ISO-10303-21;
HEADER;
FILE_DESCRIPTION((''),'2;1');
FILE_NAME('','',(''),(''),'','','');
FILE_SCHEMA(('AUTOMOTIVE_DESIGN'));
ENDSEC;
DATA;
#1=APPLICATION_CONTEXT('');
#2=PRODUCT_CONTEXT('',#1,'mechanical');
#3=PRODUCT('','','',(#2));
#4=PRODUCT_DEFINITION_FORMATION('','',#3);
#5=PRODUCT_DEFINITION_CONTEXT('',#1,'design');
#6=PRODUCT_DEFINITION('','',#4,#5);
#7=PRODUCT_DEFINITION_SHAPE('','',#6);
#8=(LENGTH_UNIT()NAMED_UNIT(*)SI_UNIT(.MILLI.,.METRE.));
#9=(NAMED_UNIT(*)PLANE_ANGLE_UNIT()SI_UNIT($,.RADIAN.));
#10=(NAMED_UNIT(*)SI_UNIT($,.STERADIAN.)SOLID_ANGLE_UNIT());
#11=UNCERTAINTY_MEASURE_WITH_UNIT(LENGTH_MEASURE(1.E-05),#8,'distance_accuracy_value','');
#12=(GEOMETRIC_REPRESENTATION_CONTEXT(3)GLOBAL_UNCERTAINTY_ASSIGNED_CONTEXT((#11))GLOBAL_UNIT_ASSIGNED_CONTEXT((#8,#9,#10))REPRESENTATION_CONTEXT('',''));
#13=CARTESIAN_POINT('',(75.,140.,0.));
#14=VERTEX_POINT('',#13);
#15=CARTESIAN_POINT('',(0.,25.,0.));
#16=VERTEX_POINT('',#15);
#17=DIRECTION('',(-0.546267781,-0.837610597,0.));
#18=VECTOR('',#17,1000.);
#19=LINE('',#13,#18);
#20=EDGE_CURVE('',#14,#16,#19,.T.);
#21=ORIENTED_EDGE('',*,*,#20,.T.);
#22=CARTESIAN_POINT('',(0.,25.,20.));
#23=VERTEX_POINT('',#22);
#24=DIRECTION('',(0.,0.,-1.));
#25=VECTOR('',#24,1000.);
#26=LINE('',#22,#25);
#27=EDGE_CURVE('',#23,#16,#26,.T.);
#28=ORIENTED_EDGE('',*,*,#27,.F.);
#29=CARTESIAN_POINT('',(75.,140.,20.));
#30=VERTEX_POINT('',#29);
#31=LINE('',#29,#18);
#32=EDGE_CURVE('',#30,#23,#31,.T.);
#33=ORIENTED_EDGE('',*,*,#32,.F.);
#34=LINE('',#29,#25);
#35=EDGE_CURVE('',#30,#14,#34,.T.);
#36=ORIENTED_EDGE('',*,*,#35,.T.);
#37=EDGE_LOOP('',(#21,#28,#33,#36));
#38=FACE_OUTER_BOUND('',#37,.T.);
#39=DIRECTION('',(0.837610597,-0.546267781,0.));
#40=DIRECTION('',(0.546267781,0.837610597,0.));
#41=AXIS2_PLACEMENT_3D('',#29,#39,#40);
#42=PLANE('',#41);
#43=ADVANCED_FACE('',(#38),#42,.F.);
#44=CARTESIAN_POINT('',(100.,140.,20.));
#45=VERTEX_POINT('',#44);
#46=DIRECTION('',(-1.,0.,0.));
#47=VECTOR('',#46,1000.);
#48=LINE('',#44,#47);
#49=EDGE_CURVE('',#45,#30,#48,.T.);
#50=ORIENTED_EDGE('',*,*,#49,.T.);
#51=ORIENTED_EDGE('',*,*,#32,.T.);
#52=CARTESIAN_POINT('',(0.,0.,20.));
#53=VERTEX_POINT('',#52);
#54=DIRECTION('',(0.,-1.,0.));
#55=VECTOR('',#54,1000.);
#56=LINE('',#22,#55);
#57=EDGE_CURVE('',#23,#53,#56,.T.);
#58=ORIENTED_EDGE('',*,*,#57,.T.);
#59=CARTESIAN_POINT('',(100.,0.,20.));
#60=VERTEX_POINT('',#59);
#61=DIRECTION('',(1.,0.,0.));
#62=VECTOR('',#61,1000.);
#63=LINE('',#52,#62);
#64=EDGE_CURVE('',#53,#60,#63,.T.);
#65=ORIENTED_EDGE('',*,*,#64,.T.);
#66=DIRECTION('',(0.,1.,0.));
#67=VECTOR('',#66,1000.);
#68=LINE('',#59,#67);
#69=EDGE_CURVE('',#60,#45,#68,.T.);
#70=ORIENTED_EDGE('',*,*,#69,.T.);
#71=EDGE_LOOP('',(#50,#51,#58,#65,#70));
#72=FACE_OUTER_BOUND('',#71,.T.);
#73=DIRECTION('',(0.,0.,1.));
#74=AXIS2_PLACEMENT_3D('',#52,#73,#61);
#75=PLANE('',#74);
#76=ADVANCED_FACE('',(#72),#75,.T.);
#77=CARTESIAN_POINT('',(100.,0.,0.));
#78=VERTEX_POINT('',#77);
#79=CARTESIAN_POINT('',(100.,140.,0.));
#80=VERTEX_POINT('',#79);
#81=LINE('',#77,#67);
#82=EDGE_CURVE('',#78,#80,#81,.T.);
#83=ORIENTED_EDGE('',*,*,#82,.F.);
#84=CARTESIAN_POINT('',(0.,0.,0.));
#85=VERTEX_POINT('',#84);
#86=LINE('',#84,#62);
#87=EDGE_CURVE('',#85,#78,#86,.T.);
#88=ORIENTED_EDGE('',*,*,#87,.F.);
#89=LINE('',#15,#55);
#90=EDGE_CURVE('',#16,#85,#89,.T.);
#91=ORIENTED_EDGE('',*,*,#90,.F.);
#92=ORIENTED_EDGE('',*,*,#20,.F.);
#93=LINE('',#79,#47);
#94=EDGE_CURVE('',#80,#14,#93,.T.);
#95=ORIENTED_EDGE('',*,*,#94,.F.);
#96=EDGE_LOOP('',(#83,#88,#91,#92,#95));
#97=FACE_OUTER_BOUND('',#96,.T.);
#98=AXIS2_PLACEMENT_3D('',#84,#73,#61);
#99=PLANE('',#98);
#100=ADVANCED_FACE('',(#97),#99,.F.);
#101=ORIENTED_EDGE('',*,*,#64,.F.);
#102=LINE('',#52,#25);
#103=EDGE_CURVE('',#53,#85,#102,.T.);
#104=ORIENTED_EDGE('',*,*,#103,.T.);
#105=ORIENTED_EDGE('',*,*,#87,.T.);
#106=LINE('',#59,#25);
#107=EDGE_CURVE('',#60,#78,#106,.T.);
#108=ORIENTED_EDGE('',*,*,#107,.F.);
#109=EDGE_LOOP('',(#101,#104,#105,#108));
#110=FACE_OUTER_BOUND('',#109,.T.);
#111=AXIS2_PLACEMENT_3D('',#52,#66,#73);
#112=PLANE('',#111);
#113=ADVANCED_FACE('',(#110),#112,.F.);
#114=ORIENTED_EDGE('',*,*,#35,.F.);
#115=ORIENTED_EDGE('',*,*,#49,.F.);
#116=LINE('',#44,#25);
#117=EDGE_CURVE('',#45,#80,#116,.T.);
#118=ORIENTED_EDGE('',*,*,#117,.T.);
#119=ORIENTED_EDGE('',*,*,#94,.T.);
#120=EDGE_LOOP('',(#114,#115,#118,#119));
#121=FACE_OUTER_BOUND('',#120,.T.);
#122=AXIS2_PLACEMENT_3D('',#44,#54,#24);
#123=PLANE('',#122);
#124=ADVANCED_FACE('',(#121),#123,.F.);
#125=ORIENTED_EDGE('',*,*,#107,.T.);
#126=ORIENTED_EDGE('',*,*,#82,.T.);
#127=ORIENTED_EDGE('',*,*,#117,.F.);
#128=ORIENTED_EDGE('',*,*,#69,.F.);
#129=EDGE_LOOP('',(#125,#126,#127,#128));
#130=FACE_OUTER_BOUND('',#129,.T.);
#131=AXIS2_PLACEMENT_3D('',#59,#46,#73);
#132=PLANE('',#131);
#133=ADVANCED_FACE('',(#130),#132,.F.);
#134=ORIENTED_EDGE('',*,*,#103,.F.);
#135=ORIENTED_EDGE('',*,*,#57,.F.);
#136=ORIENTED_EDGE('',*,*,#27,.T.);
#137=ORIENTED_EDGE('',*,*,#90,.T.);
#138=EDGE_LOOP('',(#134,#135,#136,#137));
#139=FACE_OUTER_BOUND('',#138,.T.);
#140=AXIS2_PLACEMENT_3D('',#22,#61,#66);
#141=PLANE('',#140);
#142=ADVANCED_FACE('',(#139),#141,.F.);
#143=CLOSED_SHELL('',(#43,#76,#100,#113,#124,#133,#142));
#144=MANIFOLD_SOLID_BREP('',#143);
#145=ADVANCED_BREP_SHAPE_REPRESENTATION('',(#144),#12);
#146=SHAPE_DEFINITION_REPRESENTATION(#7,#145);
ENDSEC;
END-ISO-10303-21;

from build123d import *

# Parameters (mm, degrees)
BOSS_EXTRUDE1_DEPTH = 20


with BuildPart() as part:
    # Sketch1 → Boss-Extrude1 (new body)
    with BuildSketch(Plane.XY):
        Polygon((0, 0), (100, 0), (100, 140), (75, 140), (0, 25), align=None)
    extrude(amount=BOSS_EXTRUDE1_DEPTH)


solid = part.part
